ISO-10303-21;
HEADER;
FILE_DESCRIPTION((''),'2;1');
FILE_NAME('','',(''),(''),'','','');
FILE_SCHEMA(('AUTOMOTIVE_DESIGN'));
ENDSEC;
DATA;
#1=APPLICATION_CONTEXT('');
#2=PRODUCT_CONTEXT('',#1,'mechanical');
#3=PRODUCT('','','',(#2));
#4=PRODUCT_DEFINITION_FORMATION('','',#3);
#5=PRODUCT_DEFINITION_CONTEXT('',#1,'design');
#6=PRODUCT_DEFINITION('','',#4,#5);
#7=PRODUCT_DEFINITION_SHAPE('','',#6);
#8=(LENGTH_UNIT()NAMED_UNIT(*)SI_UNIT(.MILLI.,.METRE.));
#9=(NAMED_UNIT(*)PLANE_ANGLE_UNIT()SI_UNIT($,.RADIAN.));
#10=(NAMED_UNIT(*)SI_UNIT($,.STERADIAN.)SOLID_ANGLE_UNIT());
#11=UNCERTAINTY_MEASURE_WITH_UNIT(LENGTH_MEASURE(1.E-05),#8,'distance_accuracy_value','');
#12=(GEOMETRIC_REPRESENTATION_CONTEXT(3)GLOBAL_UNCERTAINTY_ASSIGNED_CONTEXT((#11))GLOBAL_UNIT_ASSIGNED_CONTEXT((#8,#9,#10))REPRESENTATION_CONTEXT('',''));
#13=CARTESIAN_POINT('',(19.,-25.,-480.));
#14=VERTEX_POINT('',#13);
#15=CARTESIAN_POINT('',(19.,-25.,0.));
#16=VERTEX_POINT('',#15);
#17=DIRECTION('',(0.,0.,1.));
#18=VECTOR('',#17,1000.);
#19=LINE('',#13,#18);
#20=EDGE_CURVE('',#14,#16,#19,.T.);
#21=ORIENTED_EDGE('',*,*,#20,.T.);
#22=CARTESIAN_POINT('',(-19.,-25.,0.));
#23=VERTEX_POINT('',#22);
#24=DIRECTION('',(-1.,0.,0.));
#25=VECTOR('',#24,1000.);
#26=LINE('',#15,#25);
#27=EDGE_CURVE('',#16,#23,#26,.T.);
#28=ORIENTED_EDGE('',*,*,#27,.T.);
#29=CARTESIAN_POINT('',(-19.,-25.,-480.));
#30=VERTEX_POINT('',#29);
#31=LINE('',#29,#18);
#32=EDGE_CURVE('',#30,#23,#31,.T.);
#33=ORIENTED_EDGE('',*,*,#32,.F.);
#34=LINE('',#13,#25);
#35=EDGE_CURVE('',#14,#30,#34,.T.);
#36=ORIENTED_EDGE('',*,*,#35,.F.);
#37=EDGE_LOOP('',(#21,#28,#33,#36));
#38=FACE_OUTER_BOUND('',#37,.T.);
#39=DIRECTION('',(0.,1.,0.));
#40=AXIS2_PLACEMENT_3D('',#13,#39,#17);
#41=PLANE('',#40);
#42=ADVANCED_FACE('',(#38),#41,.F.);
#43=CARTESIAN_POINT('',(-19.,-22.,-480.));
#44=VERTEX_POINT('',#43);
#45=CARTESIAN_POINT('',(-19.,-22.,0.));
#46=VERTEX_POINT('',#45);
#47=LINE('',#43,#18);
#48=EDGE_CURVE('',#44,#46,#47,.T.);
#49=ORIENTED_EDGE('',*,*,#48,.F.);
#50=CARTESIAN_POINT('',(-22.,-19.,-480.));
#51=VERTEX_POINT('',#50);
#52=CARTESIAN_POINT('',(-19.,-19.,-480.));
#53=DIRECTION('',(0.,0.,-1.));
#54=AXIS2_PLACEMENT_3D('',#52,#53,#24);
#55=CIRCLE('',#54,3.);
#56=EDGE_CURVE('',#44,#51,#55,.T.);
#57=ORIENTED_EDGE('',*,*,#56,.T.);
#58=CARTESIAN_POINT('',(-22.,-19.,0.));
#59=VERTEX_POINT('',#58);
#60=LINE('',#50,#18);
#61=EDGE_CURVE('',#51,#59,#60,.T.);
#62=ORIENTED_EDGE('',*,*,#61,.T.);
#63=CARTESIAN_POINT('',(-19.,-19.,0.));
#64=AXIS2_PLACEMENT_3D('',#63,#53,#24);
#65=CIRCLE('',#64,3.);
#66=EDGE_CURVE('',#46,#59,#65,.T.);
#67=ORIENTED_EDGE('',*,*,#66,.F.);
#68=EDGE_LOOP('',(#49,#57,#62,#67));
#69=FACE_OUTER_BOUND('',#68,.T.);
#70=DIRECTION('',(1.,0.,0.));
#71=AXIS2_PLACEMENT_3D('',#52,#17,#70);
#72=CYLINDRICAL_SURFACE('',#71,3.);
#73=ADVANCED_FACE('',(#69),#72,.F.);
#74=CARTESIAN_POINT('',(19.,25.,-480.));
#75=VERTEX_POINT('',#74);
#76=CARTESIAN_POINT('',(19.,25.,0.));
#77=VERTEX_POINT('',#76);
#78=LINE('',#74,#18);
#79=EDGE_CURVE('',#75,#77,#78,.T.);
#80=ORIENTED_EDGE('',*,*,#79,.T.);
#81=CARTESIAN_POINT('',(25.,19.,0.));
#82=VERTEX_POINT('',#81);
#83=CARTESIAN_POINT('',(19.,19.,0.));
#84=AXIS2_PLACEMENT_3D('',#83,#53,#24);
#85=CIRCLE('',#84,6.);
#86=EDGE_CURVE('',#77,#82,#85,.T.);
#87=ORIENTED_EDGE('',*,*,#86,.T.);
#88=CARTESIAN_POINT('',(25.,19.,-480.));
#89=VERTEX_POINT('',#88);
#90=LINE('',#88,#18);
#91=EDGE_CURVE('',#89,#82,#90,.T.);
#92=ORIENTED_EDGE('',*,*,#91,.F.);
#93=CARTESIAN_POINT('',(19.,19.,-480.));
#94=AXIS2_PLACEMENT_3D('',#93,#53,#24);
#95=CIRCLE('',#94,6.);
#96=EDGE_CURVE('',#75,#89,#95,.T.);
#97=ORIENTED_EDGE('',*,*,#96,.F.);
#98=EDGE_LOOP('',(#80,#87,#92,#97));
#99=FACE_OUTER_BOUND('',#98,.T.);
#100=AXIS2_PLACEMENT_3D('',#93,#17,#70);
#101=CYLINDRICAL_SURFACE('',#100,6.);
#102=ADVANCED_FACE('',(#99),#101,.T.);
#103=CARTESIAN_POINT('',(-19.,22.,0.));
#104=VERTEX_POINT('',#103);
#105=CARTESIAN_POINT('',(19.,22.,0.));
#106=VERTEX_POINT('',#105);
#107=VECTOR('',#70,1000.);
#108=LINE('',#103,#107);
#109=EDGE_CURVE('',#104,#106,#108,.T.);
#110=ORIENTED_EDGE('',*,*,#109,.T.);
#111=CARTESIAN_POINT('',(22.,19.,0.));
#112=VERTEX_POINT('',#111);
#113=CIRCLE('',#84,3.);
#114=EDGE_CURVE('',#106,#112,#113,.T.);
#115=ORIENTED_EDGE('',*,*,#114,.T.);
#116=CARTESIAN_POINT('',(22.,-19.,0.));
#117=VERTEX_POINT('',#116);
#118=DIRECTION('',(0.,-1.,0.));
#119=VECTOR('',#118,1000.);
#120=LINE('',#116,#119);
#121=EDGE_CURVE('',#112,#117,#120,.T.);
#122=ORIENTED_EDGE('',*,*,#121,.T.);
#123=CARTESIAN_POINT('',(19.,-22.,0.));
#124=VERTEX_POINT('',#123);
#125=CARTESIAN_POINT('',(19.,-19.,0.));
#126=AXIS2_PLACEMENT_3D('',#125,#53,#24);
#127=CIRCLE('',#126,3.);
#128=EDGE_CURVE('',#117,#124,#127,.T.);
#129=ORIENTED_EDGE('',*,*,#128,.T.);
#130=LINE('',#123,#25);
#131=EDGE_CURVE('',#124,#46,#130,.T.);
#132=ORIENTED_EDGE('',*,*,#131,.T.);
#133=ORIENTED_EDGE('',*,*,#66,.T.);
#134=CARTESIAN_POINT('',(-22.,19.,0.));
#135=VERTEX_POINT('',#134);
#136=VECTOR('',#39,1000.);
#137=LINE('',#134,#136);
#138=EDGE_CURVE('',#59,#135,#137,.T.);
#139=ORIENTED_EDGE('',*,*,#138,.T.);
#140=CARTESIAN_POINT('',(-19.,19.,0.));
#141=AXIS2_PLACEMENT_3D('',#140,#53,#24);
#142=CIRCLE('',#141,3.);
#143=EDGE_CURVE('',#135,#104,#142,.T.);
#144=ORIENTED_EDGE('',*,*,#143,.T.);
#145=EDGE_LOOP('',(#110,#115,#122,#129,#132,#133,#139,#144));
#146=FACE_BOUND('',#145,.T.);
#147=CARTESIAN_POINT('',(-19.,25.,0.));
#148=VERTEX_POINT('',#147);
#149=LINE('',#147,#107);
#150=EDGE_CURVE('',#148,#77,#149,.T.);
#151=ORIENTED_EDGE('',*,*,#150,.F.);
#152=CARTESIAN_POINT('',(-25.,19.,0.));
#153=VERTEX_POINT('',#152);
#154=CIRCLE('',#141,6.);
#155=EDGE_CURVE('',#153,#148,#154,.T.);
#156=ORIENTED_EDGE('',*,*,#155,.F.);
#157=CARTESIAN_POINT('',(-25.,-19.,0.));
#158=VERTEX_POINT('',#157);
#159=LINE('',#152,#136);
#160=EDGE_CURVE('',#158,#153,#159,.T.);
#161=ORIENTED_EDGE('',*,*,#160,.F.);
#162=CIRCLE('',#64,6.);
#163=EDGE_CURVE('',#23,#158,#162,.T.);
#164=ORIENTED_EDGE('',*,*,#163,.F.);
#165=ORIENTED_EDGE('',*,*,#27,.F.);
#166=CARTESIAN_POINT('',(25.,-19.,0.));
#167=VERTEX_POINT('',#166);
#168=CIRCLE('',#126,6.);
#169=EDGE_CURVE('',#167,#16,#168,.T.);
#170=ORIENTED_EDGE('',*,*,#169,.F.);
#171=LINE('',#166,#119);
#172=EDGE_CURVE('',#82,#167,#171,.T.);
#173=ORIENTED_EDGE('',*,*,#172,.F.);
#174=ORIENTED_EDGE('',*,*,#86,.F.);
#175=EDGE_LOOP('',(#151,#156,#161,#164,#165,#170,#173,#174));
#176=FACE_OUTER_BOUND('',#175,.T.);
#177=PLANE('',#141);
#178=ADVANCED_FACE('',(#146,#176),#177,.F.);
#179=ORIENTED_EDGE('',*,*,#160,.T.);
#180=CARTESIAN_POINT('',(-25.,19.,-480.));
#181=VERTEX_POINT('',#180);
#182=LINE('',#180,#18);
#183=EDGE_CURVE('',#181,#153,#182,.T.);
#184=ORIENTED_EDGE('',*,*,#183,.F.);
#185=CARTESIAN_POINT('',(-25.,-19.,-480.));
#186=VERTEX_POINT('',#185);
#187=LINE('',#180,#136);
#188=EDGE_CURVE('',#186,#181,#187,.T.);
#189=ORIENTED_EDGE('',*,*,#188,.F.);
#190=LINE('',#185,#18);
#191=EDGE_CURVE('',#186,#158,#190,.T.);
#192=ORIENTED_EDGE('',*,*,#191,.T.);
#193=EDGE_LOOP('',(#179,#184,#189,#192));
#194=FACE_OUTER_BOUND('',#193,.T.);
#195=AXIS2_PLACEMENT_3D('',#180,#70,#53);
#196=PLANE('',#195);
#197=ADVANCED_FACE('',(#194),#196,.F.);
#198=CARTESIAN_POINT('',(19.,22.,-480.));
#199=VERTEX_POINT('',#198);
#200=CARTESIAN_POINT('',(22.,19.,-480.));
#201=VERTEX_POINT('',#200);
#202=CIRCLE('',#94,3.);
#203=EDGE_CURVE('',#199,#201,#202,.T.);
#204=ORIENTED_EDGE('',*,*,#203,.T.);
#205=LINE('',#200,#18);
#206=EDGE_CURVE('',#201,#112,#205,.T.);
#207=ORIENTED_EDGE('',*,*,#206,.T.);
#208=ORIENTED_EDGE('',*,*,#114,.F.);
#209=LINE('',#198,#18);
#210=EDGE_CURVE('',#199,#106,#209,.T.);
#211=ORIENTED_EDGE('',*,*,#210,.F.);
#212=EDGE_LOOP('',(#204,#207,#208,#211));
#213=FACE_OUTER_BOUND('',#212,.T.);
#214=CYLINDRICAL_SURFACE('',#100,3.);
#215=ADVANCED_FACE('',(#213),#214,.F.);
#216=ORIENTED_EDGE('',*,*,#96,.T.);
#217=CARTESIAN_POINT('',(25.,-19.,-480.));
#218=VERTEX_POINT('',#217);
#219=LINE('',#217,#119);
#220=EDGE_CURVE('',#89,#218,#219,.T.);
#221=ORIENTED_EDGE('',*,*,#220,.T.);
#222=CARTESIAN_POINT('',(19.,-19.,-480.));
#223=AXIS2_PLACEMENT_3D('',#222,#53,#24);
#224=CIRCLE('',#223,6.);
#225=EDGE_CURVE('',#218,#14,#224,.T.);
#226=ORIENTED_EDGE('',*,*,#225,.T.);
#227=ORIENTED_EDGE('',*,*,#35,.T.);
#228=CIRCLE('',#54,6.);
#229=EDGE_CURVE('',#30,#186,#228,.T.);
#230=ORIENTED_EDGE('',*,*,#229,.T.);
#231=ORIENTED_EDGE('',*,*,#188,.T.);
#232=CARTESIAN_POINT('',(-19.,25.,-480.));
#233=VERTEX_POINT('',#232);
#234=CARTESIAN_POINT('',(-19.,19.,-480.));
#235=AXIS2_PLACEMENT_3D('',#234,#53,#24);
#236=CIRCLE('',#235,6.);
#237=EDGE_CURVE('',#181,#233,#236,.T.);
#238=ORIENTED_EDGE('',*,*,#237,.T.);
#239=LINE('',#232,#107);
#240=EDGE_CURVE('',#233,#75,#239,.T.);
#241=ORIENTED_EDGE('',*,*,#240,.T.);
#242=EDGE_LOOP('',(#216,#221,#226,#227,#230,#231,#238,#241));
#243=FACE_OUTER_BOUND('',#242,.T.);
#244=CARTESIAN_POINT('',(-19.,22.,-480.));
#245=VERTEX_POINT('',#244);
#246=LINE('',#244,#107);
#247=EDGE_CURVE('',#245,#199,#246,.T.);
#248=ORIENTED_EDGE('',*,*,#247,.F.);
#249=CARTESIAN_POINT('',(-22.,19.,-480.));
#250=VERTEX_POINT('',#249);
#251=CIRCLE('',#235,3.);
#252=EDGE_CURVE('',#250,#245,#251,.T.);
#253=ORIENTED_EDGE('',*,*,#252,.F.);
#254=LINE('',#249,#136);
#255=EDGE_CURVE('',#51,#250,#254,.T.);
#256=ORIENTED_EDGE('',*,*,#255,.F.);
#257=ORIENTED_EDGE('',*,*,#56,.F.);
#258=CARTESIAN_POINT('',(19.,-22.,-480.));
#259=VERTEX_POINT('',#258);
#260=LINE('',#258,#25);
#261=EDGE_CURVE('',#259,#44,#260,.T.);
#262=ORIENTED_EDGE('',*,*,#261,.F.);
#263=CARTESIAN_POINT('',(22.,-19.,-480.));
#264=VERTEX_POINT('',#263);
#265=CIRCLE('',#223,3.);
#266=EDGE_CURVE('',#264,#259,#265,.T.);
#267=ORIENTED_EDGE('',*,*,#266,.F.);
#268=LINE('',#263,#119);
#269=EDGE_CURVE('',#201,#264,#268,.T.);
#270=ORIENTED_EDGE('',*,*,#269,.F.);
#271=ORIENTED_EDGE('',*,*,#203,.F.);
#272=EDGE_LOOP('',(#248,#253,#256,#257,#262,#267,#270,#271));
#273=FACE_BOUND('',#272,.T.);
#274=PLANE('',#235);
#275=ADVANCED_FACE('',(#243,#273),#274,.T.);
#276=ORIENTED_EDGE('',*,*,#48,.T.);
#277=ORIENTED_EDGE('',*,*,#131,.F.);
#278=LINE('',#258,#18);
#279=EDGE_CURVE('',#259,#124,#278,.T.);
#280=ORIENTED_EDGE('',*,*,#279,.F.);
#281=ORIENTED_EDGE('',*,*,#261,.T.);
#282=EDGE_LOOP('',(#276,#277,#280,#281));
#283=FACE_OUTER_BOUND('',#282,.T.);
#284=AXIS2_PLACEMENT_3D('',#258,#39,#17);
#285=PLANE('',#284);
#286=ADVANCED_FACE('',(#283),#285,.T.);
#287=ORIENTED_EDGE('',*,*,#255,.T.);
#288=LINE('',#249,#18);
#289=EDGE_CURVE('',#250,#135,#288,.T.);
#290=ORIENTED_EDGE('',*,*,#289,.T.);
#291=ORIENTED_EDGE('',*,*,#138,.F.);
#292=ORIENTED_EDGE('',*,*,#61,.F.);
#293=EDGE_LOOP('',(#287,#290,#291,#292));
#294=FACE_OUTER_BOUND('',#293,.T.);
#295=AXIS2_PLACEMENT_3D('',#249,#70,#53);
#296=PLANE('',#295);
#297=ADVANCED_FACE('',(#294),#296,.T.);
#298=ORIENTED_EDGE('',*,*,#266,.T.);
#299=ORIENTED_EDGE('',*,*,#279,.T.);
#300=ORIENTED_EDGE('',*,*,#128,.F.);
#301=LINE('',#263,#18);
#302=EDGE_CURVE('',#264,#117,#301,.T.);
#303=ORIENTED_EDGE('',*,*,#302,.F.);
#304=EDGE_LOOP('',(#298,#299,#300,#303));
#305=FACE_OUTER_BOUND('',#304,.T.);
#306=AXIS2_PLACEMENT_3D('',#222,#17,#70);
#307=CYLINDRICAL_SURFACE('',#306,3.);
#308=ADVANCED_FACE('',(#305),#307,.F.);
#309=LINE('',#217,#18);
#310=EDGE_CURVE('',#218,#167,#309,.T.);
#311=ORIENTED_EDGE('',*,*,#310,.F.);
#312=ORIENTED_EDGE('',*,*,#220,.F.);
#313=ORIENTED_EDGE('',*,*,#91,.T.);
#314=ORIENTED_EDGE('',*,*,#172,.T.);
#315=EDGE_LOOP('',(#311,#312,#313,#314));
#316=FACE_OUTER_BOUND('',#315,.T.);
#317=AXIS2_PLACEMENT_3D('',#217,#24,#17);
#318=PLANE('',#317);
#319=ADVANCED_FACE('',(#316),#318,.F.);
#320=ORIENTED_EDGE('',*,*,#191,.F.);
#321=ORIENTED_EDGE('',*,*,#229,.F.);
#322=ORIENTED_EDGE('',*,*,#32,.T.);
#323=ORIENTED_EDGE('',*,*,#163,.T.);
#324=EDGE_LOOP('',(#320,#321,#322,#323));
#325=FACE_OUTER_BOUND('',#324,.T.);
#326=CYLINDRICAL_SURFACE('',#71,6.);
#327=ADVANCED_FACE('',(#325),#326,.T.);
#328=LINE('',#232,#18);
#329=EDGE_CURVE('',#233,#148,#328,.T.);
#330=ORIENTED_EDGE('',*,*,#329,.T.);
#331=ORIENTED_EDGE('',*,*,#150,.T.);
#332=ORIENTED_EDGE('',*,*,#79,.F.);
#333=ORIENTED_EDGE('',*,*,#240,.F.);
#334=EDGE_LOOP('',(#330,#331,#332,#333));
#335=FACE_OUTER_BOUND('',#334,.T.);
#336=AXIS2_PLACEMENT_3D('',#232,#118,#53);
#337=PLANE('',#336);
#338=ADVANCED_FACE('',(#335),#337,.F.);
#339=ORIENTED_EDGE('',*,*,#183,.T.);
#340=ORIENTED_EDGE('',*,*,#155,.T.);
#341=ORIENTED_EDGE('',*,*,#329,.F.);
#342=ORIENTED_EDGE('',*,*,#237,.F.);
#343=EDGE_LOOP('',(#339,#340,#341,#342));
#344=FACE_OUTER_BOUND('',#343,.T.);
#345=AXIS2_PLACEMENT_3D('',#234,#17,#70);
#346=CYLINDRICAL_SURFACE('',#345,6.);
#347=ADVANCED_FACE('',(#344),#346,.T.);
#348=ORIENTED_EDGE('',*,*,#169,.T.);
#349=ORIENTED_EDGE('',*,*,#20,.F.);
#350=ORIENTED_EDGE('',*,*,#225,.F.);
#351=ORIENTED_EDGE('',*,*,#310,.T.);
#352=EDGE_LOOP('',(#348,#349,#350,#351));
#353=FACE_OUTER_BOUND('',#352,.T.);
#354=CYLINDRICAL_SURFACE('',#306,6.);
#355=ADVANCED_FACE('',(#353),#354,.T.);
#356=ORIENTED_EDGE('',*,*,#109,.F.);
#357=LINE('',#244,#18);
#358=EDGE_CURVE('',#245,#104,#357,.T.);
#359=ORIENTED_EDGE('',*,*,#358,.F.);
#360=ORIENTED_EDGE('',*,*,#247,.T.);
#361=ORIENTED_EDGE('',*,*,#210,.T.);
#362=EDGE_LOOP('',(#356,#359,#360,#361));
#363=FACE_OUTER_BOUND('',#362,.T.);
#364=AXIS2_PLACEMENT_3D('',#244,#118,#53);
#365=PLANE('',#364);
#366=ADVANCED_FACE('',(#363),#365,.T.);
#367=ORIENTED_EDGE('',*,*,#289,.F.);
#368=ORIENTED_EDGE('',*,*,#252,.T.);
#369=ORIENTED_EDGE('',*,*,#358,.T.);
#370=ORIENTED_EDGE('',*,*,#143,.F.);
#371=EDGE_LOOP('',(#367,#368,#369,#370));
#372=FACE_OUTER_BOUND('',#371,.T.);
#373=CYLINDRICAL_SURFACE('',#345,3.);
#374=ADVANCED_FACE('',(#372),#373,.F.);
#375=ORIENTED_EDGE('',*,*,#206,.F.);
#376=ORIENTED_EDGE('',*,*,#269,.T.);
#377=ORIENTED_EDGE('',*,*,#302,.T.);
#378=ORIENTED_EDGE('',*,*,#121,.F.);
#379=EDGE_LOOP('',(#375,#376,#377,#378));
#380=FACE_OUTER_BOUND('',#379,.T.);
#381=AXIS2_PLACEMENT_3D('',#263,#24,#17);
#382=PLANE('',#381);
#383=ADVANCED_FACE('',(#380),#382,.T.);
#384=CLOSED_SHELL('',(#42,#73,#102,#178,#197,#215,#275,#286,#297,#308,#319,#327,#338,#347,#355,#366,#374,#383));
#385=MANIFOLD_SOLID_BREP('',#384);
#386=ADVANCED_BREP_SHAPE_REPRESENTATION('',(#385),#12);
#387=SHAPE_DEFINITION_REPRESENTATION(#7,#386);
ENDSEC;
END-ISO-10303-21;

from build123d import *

# Parameters (mm, degrees)
GB_6728_1986_050_X_50_X_3_1_DEPTH = 480


with BuildPart() as part:
    # Sketch1 → Gb／6728-1986方形空心型钢 050 X 50 X 3(1) (new body)
    with BuildSketch(Plane(origin=(0, 0, 0), x_dir=(-1, 0, 0), z_dir=(0, 0, -1))):
        with BuildLine():
            Line((-19, -25), (19, -25))
            ThreePointArc((19, -25), (23.242640687, -23.242640687), (25, -19))
            Line((25, -19), (25, 19))
            ThreePointArc((25, 19), (23.242640687, 23.242640687), (19, 25))
            Line((19, 25), (-19, 25))
            ThreePointArc((-19, 25), (-23.242640687, 23.242640687), (-25, 19))
            Line((-25, 19), (-25, -19))
            ThreePointArc((-25, -19), (-23.242640687, -23.242640687), (-19, -25))
        make_face()
        with BuildLine():
            Line((-19, -22), (19, -22))
            ThreePointArc((19, -22), (21.121320344, -21.121320344), (22, -19))
            Line((22, -19), (22, 19))
            ThreePointArc((22, 19), (21.121320344, 21.121320344), (19, 22))
            Line((19, 22), (-19, 22))
            ThreePointArc((-19, 22), (-21.121320344, 21.121320344), (-22, 19))
            Line((-22, 19), (-22, -19))
            ThreePointArc((-22, -19), (-21.121320344, -21.121320344), (-19, -22))
        make_face(mode=Mode.SUBTRACT)
    extrude(amount=GB_6728_1986_050_X_50_X_3_1_DEPTH)


solid = part.part
